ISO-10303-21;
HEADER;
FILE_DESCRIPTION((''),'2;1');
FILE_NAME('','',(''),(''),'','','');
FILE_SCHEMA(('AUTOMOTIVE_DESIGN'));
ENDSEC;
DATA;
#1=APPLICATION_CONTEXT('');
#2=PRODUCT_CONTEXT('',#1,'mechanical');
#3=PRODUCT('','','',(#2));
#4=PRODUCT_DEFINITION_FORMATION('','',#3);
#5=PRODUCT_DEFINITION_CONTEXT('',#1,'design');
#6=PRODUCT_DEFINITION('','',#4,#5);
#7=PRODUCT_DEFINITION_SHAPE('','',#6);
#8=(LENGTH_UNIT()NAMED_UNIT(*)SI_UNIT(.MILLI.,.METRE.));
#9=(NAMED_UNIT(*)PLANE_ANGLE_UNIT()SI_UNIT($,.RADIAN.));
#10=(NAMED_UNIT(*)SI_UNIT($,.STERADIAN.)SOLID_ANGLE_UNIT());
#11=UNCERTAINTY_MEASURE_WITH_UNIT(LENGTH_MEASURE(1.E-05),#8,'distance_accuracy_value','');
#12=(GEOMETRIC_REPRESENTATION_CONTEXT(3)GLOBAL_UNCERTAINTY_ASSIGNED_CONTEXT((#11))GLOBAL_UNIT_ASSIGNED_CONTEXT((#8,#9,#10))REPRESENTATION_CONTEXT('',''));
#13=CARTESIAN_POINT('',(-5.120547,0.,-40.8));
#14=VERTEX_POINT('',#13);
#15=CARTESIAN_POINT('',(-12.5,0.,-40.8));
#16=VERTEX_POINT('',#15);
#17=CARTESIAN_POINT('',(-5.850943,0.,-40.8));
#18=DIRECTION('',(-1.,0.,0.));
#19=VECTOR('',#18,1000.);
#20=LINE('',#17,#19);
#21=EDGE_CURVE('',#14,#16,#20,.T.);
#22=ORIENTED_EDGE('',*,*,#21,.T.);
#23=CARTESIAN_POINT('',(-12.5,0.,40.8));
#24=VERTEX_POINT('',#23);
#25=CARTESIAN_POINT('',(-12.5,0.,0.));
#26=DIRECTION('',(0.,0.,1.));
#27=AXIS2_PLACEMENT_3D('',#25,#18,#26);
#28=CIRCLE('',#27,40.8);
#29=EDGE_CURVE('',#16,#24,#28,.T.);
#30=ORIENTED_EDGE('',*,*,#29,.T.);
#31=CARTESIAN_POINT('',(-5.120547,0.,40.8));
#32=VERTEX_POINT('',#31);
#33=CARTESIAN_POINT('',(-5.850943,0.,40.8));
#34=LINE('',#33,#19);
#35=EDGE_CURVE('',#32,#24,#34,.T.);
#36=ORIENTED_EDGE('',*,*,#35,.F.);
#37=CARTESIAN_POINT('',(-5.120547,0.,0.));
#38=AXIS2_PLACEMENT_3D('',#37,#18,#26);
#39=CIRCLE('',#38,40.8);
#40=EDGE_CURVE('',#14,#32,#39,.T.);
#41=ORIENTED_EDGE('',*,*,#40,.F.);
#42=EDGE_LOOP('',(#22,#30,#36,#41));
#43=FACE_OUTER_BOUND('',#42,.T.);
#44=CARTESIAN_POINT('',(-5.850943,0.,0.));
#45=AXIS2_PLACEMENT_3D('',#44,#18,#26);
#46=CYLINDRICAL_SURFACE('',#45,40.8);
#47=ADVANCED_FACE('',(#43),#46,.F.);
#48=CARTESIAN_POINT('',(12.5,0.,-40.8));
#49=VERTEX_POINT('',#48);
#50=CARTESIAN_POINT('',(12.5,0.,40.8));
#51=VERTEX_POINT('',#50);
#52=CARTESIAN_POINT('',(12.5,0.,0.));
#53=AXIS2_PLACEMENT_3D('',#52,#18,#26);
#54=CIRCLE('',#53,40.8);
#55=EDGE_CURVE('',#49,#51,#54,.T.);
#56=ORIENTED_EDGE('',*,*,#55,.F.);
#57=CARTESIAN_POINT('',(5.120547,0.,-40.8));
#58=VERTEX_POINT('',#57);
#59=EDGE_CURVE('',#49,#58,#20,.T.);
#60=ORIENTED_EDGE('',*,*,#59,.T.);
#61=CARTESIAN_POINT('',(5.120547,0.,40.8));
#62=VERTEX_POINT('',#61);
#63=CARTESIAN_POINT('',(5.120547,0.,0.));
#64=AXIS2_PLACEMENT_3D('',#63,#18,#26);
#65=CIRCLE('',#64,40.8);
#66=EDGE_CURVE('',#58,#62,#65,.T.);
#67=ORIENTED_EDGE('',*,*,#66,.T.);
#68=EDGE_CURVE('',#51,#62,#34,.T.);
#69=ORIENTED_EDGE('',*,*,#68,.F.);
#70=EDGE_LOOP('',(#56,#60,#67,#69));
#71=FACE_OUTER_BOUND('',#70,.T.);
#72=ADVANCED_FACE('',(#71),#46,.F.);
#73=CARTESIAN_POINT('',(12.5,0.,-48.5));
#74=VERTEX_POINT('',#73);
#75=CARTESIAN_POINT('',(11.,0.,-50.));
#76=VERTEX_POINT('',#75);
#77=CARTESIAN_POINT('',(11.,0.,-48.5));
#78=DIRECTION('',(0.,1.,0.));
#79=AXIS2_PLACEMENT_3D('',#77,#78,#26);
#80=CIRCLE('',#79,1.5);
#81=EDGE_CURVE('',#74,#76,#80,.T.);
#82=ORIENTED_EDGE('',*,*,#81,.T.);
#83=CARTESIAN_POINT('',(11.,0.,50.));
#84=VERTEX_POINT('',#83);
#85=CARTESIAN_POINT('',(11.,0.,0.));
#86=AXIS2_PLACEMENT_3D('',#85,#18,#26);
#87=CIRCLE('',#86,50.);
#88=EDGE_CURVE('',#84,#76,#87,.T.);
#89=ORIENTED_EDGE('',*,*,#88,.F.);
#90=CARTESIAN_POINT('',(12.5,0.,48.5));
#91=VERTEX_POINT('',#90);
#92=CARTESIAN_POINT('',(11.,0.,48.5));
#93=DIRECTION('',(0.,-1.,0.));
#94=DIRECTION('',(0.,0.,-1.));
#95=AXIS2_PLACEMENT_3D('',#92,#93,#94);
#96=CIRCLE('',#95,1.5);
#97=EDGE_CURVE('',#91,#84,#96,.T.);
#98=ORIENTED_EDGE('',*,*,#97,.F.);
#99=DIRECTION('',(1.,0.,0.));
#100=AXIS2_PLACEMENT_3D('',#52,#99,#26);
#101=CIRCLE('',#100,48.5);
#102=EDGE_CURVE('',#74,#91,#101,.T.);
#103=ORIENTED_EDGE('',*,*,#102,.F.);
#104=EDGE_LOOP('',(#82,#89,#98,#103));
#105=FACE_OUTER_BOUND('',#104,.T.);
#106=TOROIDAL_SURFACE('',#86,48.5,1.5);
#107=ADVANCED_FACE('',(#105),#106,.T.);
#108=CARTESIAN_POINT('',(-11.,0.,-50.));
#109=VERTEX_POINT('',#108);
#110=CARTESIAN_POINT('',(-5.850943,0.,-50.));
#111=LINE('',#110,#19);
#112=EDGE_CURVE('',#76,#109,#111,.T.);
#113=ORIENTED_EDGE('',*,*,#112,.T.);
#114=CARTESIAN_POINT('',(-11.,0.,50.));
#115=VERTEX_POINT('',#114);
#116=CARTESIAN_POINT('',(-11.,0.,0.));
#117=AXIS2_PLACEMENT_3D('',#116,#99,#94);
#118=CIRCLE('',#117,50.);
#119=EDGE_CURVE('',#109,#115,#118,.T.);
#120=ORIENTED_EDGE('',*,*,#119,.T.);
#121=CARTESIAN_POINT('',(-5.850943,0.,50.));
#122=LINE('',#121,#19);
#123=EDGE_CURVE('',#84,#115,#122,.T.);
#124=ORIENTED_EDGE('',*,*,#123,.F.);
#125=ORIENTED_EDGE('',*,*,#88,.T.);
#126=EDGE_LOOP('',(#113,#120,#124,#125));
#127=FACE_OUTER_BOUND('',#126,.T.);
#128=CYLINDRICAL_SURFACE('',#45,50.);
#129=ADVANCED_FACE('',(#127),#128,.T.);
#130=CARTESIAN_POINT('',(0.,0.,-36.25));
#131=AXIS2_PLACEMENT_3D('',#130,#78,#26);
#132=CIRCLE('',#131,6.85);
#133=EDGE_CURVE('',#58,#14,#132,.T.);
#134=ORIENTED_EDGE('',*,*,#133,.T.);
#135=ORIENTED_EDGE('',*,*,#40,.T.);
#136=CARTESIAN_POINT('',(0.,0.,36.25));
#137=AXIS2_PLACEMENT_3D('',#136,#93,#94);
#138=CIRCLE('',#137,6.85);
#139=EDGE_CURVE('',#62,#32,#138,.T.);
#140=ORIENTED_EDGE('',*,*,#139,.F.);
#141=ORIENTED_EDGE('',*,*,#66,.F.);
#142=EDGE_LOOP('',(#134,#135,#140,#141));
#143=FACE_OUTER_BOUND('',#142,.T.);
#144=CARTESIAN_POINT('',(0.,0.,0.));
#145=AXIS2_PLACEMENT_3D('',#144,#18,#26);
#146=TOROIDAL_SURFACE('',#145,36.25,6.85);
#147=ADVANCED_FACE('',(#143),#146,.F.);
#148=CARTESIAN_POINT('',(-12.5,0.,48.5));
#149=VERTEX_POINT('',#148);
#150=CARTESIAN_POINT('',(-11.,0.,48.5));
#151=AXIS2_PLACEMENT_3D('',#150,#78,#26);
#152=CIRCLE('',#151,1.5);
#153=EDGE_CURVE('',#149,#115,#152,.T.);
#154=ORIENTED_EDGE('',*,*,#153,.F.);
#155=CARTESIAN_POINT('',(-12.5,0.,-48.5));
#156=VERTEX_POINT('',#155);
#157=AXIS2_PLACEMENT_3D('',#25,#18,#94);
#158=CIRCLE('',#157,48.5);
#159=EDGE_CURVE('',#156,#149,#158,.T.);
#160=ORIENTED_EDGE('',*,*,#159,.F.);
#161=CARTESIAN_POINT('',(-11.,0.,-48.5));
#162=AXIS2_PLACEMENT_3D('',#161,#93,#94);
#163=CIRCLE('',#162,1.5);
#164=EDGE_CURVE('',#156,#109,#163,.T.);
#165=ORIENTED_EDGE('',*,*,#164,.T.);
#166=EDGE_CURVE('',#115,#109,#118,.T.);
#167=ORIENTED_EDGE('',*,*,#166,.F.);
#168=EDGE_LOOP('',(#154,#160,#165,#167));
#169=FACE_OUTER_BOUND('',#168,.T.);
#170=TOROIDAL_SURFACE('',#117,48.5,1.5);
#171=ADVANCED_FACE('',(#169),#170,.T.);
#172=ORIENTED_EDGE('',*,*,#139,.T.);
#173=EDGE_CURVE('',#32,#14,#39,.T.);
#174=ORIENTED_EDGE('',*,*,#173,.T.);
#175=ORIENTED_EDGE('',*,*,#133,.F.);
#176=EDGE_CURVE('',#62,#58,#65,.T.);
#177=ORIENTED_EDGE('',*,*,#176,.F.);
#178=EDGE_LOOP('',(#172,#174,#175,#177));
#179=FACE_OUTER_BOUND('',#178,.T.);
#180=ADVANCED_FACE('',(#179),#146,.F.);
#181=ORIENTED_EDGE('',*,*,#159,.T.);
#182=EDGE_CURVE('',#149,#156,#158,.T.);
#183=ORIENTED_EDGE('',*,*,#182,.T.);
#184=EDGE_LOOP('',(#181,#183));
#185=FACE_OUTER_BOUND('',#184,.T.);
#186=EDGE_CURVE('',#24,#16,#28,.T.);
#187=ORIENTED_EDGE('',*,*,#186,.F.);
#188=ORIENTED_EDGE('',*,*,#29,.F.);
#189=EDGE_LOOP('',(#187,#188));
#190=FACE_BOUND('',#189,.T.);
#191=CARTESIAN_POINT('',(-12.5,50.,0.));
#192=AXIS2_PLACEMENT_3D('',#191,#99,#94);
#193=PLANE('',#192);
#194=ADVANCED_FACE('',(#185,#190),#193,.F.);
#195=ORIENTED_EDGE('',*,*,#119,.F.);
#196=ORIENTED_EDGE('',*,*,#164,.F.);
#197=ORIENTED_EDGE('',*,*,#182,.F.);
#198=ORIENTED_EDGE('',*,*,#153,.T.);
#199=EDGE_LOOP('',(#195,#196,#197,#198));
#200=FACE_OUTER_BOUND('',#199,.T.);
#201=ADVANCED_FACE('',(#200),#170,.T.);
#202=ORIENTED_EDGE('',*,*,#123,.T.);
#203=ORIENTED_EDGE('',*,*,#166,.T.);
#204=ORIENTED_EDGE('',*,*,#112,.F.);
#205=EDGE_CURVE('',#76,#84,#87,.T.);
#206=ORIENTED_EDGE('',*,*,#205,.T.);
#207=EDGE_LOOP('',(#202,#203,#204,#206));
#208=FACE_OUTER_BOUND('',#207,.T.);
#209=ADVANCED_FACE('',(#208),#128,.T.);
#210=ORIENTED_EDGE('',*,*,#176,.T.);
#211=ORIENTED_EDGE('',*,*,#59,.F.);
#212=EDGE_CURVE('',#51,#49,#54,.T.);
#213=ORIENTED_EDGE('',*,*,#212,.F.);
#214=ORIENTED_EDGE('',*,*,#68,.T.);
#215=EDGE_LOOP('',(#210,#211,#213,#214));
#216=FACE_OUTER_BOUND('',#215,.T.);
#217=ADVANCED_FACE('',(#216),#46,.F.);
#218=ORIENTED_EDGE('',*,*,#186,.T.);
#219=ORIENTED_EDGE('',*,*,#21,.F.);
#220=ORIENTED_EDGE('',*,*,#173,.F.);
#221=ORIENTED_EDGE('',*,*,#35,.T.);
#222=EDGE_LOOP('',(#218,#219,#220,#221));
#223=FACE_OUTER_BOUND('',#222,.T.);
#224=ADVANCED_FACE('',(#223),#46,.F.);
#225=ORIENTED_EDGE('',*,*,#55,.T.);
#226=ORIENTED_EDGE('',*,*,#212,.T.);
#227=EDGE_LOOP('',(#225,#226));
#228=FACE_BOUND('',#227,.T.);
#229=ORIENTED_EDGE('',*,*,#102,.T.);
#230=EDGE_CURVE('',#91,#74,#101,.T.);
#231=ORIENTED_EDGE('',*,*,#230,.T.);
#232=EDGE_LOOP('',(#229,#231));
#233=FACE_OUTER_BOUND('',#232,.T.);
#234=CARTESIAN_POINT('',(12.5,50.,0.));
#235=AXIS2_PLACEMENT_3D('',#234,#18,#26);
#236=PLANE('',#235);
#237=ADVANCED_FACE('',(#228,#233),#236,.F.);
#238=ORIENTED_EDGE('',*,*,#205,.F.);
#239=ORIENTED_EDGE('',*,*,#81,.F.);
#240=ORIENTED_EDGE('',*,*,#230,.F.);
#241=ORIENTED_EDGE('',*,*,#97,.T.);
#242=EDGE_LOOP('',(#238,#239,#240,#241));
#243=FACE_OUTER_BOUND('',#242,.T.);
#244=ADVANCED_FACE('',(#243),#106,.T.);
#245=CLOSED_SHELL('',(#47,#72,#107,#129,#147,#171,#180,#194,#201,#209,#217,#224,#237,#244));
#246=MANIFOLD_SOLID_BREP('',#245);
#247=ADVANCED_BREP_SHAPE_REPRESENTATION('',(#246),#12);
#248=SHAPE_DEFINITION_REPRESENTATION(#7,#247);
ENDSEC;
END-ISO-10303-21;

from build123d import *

# Parameters (mm, degrees)
FILLET1_R = 1.5


with BuildPart() as part:
    # Sketch1 → Revolve1 (revolve)
    with BuildSketch(Plane.XY, mode=Mode.PRIVATE) as revolve1_sk:
        with BuildLine():
            Line((5.120546846, 40.8), (12.5, 40.8))
            Line((12.5, 40.8), (12.5, 50))
            Line((12.5, 50), (-12.5, 50))
            Line((-12.5, 50), (-12.5, 40.8))
            Line((-12.5, 40.8), (-5.120546846, 40.8))
            ThreePointArc((-5.120546846, 40.8), (0, 43.1), (5.120546846, 40.8))
        make_face()
    revolve(revolve1_sk.sketch.rotate(Axis((-5.850943074, 0, 0), (1, 0, 0)), 90), axis=Axis((-5.850943074, 0, 0), (1, 0, 0)))

    # Fillet1
    fillet1_edges = [part.edges().sort_by_distance(p)[0] for p in [
        (-12.5, 0, -50),
        (12.5, 0, -50),
    ]]
    fillet(fillet1_edges, radius=FILLET1_R)


solid = part.part
